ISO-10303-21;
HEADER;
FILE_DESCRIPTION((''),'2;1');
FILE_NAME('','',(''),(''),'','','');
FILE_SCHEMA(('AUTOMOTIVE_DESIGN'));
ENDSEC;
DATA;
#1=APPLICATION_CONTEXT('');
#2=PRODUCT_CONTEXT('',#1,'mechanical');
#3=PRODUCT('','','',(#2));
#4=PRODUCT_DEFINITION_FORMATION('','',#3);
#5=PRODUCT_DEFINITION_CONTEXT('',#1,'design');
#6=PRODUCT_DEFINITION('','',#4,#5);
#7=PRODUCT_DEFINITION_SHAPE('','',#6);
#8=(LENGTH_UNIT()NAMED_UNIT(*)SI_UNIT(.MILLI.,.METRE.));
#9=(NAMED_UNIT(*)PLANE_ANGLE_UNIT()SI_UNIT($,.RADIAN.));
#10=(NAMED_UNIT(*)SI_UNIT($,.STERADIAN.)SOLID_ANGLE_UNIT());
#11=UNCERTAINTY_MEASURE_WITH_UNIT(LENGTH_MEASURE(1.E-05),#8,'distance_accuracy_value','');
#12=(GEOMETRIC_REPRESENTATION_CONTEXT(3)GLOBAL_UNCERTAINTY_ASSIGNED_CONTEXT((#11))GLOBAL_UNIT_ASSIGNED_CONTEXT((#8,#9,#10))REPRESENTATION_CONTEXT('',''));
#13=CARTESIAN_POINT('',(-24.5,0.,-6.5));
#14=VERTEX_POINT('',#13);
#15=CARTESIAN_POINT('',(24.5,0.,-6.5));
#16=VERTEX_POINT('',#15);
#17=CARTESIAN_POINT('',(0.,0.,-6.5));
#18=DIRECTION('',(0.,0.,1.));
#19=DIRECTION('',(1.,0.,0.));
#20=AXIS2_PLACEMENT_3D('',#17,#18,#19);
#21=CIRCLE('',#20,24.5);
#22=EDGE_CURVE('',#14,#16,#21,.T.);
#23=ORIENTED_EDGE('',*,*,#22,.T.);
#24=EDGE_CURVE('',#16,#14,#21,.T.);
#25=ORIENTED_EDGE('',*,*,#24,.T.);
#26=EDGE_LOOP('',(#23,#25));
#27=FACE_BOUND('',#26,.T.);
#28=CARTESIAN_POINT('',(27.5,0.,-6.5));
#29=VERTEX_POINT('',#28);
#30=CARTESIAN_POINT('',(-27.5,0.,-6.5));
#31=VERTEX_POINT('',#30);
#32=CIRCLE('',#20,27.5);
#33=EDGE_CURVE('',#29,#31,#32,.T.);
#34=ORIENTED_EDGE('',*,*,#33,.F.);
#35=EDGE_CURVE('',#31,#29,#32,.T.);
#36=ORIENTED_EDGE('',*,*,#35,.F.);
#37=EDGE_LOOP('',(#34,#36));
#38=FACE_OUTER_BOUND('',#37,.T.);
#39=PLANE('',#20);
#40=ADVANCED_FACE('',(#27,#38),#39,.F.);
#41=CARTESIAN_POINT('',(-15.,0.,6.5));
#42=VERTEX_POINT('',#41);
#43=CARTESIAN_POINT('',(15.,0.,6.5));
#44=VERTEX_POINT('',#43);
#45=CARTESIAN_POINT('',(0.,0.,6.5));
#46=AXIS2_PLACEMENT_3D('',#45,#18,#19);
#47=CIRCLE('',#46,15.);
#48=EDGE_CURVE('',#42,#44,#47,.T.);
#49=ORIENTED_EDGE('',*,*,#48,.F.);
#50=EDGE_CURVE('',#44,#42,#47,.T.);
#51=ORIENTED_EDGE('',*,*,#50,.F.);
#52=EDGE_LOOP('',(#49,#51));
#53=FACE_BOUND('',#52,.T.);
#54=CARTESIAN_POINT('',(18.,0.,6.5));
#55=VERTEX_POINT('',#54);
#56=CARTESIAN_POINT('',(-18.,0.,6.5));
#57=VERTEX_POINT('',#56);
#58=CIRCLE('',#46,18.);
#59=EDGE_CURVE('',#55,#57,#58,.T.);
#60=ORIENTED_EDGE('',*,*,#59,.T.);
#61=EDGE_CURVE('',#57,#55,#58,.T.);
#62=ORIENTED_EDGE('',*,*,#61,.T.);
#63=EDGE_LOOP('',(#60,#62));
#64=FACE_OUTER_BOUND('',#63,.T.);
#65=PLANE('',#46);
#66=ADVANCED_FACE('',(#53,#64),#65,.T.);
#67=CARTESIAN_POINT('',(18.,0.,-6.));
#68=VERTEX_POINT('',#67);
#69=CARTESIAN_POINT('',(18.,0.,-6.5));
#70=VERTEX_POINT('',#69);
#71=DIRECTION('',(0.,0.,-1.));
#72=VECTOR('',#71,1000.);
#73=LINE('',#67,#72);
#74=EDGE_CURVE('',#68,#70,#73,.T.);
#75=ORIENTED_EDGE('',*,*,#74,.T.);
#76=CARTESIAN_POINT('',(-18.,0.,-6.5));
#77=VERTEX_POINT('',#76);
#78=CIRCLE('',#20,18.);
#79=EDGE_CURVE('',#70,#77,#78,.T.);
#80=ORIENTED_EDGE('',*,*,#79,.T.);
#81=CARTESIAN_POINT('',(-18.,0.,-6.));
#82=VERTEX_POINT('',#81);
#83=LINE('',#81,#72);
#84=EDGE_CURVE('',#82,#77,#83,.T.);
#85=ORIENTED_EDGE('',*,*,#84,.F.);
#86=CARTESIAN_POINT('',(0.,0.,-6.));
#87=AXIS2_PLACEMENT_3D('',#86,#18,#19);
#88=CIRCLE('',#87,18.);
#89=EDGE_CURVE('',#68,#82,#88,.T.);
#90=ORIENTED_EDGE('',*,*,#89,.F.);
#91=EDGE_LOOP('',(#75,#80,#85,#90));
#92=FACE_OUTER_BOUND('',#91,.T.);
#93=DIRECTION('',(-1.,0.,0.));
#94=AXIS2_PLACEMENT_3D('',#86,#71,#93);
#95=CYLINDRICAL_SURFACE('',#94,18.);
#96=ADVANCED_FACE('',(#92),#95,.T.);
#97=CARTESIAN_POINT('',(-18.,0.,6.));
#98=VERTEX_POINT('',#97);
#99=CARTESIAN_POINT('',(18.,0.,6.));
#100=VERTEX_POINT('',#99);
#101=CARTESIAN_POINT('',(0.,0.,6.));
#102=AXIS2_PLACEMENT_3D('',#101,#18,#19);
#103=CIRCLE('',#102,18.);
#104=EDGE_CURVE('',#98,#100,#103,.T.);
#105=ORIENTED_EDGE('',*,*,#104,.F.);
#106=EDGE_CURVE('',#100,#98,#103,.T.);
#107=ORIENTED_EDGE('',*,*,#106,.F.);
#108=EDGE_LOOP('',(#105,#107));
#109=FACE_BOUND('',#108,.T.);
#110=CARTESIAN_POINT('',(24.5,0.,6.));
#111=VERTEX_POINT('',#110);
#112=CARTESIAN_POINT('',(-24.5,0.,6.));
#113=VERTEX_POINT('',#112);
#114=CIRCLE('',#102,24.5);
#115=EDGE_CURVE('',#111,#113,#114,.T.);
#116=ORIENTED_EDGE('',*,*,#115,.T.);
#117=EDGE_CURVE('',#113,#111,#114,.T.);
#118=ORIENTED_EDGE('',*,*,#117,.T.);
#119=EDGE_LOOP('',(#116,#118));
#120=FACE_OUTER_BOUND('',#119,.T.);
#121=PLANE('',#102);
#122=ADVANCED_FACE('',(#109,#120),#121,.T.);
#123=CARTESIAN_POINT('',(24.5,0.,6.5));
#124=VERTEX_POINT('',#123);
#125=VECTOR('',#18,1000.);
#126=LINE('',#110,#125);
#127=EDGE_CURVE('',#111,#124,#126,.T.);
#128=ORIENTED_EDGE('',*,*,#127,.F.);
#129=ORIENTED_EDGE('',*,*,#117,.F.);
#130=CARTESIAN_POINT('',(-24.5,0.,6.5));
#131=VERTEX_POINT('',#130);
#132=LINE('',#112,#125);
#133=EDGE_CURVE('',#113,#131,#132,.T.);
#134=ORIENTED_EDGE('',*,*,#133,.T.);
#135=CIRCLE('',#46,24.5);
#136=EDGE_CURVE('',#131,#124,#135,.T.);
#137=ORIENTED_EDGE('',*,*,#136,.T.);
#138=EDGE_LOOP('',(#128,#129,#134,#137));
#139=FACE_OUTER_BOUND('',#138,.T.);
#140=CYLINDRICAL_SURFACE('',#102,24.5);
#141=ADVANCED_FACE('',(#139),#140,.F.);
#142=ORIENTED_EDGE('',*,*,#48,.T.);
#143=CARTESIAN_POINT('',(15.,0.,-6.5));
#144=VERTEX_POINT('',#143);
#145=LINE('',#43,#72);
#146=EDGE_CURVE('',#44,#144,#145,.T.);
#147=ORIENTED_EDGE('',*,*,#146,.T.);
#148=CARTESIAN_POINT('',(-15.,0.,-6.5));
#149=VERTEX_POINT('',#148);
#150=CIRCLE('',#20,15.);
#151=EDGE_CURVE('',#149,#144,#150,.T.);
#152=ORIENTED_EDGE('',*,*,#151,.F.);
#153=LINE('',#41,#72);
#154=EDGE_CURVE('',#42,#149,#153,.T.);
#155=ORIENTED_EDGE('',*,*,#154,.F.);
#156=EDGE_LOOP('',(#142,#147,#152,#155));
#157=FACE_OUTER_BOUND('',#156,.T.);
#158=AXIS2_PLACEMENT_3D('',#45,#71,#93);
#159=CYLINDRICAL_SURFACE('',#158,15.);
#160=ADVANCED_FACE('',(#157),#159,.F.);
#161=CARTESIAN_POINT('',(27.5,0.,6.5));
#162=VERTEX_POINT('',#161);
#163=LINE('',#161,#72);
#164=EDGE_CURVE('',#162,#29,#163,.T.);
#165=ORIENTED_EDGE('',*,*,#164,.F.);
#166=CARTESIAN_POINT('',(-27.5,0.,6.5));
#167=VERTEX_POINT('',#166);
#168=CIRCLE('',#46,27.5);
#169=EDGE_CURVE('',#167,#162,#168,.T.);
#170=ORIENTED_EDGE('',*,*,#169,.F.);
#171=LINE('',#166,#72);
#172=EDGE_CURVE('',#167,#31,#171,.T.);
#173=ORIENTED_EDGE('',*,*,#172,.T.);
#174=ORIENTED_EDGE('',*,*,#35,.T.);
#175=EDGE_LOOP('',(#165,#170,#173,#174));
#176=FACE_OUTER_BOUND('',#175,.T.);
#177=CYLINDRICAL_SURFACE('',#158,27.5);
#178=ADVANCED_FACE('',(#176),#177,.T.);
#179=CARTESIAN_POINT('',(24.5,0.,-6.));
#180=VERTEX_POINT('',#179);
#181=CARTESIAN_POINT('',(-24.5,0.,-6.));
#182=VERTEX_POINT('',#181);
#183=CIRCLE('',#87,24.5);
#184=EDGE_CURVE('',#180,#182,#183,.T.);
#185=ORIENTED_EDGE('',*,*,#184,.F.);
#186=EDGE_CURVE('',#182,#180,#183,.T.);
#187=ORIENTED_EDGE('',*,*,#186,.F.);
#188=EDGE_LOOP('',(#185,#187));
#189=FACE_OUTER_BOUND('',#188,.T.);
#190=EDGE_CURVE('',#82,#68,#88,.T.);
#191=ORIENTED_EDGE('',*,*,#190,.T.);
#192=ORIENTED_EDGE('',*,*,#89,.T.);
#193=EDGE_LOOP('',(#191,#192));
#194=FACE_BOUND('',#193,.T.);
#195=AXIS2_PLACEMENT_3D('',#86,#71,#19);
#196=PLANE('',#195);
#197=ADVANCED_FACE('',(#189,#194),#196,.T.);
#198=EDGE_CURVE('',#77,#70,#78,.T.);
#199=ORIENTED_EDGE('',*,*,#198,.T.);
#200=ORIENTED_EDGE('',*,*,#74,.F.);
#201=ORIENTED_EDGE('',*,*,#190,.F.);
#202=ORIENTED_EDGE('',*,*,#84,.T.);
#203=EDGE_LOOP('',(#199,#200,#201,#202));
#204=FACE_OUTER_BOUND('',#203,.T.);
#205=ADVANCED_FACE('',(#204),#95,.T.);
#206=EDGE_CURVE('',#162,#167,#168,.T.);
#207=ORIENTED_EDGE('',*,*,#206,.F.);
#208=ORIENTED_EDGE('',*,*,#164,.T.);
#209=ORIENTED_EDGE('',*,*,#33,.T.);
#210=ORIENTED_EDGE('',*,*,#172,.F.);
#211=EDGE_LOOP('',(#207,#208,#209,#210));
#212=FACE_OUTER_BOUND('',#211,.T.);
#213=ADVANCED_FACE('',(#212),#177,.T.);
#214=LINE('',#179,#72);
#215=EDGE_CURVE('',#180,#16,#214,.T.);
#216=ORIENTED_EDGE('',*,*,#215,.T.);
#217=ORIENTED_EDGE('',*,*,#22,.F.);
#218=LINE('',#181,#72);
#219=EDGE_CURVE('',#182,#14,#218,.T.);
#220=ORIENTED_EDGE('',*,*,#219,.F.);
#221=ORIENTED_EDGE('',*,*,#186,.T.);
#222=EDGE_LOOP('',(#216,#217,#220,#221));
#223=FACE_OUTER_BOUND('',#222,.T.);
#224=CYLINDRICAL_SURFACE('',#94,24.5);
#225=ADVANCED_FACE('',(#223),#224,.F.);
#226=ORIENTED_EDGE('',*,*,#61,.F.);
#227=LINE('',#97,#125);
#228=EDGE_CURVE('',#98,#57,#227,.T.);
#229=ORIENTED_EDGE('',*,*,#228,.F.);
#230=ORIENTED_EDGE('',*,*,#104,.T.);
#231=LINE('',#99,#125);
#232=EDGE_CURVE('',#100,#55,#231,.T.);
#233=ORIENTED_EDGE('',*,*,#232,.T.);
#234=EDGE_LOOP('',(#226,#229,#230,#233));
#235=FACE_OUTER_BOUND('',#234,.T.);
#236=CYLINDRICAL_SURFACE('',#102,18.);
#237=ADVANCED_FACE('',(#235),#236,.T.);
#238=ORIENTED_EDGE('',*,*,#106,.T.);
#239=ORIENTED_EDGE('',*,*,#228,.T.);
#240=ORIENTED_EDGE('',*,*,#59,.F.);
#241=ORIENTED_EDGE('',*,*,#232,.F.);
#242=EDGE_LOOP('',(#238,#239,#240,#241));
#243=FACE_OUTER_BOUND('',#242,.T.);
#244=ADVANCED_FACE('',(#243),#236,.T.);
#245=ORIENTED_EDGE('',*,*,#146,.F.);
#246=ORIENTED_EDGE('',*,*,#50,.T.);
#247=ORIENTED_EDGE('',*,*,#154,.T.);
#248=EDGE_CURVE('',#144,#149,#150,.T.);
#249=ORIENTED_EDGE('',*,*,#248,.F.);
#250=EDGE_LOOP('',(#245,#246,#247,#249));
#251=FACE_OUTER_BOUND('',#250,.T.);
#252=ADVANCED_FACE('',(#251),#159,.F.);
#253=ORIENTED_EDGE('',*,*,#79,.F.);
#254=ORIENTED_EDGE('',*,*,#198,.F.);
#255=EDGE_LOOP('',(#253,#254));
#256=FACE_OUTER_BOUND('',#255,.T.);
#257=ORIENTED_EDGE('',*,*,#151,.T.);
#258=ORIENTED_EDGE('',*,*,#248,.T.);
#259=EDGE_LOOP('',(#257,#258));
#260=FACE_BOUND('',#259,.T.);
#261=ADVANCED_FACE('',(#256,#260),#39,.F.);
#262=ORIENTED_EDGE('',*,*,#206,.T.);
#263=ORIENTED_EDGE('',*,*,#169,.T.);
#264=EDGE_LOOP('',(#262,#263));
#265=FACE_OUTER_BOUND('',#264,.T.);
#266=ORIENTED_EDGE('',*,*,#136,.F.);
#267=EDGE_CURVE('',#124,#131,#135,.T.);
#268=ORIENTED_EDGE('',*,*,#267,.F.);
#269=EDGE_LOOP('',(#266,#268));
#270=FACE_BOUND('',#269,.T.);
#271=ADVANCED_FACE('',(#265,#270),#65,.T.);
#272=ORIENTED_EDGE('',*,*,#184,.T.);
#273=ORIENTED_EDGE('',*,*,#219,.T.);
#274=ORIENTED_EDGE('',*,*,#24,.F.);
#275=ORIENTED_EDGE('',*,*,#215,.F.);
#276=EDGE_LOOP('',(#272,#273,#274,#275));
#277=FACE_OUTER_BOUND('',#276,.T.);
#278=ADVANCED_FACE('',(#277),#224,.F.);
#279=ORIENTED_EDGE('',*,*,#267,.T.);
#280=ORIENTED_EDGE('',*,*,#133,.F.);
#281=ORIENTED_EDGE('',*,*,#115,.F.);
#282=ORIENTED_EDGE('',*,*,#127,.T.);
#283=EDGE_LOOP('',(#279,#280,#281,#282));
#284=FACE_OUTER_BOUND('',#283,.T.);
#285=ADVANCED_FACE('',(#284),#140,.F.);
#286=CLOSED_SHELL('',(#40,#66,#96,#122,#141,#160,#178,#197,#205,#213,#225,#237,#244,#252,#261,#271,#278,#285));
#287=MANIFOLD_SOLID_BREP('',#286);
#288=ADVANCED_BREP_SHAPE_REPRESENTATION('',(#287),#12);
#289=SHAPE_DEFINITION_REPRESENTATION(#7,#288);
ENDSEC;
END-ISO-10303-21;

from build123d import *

# Parameters (mm, degrees)
SKETCH1_R           = 27.5
SKETCH1_R_2         = 15
BOSS_EXTRUDE1_DEPTH = 6.5
SKETCH2_R           = 24.5
SKETCH2_R_2         = 18
CUT_EXTRUDE1_DEPTH  = 0.5


with BuildPart() as part:
    # Sketch1 → Boss-Extrude1 (new, symmetric)
    with BuildSketch(Plane.XY):
        with Locations(Location((0, 0, 0), (0, 0, 180))):
            Circle(SKETCH1_R)
        with Locations(Location((0, 0, 0), (0, 0, 180))):
            Circle(SKETCH1_R_2, mode=Mode.SUBTRACT)
    extrude(amount=BOSS_EXTRUDE1_DEPTH, both=True)

    # Sketch2 → Cut-Extrude1 (cut)
    with BuildSketch(Plane.XY.offset(6.5)):
        Circle(SKETCH2_R)
        Circle(SKETCH2_R_2, mode=Mode.SUBTRACT)
    cut_extrude1 = extrude(amount=-CUT_EXTRUDE1_DEPTH, mode=Mode.SUBTRACT)

    # Mirror1: Cut-Extrude1 across plane
    add(cut_extrude1.mirror(Plane.XY), mode=Mode.SUBTRACT)


solid = part.part
